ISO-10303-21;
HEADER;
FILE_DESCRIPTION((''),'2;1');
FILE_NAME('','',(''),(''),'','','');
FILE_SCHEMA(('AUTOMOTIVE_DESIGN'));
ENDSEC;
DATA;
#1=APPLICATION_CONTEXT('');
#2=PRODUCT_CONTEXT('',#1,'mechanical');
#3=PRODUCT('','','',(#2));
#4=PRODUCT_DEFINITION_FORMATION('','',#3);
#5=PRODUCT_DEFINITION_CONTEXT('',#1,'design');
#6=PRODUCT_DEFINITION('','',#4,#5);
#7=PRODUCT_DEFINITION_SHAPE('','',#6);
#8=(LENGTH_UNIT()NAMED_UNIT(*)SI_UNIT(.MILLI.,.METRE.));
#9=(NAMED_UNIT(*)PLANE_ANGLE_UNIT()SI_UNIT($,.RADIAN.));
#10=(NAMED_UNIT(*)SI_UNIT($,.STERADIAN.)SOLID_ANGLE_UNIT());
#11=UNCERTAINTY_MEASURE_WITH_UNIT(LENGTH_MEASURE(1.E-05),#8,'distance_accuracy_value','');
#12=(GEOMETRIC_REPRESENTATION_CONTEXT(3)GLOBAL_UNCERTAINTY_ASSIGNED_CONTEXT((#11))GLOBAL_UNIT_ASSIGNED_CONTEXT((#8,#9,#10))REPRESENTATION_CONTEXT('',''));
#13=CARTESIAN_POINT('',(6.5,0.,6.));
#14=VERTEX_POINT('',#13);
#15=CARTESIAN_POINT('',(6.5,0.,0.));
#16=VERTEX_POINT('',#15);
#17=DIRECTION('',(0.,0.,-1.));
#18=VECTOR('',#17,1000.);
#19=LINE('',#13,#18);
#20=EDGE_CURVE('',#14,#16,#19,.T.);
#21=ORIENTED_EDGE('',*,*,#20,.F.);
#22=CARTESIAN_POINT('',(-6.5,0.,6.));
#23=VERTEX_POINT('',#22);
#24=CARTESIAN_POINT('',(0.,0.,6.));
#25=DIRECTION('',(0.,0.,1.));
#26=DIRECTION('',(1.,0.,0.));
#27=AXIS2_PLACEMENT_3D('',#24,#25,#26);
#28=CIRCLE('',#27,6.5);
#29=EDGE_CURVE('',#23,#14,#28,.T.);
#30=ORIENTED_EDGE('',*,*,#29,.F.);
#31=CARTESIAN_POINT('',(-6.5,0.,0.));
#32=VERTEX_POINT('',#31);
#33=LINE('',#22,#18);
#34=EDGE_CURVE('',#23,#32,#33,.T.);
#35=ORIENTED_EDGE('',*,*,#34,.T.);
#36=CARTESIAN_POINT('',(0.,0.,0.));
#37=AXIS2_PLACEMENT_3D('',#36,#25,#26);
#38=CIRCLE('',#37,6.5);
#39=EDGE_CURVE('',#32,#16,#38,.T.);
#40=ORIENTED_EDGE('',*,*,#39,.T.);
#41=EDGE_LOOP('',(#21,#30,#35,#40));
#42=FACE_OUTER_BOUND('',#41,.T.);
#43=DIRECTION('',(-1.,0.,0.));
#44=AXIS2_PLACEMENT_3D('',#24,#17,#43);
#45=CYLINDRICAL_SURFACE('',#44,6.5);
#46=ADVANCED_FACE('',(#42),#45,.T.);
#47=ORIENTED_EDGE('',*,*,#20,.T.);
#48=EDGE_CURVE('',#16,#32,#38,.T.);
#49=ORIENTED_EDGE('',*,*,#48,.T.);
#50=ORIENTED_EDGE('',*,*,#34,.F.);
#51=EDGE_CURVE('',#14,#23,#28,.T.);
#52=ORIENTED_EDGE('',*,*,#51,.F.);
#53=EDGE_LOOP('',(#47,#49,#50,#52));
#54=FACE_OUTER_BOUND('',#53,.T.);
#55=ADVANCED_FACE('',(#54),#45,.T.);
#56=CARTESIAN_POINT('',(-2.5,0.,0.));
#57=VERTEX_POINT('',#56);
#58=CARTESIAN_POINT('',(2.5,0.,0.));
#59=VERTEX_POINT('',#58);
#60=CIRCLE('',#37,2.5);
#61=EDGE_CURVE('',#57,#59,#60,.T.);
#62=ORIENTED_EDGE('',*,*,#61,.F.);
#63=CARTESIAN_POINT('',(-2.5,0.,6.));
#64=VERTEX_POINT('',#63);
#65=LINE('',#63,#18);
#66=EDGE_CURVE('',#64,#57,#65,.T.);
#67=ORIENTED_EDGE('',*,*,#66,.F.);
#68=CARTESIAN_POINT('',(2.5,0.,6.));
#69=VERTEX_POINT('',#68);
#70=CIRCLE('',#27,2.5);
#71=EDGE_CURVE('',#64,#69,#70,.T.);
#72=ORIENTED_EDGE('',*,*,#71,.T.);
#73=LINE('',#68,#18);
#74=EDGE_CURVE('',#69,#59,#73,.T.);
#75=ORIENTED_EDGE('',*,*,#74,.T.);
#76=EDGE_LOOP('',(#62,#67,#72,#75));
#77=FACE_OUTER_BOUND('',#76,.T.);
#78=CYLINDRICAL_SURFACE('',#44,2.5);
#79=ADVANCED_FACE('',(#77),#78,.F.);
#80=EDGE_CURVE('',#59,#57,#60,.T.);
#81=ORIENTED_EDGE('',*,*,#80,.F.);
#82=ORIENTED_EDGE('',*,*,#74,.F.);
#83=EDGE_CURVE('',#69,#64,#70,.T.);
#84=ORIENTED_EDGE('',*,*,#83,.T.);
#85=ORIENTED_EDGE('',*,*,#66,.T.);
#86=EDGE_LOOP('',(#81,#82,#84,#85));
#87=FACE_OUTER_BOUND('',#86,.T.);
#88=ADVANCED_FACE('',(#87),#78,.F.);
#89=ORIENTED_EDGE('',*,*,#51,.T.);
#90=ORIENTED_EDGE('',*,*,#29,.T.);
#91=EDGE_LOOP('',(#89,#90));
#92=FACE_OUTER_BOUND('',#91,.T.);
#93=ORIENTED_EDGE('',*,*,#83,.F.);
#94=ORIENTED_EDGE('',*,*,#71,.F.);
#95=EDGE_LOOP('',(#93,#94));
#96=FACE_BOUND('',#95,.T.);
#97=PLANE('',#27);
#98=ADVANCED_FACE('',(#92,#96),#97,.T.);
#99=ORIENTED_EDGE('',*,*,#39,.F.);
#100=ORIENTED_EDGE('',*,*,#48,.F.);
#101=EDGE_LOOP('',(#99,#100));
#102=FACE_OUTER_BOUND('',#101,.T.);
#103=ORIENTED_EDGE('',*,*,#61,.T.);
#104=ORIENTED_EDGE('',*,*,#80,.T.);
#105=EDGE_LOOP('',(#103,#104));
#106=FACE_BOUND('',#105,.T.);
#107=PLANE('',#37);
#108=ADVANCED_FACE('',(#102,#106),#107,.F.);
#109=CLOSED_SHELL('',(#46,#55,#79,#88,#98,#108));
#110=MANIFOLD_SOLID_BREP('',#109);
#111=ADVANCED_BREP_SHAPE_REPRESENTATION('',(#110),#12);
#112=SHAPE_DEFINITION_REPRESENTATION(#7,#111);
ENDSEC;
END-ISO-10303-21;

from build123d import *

# Parameters (mm, degrees)
SKETCH2_R           = 6.5
SKETCH2_R_2         = 2.5
BOSS_EXTRUDE1_DEPTH = 6


with BuildPart() as part:
    # Sketch2 → Boss-Extrude1 (new body)
    with BuildSketch(Plane.XY):
        Circle(SKETCH2_R)
        Circle(SKETCH2_R_2, mode=Mode.SUBTRACT)
    extrude(amount=BOSS_EXTRUDE1_DEPTH)


solid = part.part
